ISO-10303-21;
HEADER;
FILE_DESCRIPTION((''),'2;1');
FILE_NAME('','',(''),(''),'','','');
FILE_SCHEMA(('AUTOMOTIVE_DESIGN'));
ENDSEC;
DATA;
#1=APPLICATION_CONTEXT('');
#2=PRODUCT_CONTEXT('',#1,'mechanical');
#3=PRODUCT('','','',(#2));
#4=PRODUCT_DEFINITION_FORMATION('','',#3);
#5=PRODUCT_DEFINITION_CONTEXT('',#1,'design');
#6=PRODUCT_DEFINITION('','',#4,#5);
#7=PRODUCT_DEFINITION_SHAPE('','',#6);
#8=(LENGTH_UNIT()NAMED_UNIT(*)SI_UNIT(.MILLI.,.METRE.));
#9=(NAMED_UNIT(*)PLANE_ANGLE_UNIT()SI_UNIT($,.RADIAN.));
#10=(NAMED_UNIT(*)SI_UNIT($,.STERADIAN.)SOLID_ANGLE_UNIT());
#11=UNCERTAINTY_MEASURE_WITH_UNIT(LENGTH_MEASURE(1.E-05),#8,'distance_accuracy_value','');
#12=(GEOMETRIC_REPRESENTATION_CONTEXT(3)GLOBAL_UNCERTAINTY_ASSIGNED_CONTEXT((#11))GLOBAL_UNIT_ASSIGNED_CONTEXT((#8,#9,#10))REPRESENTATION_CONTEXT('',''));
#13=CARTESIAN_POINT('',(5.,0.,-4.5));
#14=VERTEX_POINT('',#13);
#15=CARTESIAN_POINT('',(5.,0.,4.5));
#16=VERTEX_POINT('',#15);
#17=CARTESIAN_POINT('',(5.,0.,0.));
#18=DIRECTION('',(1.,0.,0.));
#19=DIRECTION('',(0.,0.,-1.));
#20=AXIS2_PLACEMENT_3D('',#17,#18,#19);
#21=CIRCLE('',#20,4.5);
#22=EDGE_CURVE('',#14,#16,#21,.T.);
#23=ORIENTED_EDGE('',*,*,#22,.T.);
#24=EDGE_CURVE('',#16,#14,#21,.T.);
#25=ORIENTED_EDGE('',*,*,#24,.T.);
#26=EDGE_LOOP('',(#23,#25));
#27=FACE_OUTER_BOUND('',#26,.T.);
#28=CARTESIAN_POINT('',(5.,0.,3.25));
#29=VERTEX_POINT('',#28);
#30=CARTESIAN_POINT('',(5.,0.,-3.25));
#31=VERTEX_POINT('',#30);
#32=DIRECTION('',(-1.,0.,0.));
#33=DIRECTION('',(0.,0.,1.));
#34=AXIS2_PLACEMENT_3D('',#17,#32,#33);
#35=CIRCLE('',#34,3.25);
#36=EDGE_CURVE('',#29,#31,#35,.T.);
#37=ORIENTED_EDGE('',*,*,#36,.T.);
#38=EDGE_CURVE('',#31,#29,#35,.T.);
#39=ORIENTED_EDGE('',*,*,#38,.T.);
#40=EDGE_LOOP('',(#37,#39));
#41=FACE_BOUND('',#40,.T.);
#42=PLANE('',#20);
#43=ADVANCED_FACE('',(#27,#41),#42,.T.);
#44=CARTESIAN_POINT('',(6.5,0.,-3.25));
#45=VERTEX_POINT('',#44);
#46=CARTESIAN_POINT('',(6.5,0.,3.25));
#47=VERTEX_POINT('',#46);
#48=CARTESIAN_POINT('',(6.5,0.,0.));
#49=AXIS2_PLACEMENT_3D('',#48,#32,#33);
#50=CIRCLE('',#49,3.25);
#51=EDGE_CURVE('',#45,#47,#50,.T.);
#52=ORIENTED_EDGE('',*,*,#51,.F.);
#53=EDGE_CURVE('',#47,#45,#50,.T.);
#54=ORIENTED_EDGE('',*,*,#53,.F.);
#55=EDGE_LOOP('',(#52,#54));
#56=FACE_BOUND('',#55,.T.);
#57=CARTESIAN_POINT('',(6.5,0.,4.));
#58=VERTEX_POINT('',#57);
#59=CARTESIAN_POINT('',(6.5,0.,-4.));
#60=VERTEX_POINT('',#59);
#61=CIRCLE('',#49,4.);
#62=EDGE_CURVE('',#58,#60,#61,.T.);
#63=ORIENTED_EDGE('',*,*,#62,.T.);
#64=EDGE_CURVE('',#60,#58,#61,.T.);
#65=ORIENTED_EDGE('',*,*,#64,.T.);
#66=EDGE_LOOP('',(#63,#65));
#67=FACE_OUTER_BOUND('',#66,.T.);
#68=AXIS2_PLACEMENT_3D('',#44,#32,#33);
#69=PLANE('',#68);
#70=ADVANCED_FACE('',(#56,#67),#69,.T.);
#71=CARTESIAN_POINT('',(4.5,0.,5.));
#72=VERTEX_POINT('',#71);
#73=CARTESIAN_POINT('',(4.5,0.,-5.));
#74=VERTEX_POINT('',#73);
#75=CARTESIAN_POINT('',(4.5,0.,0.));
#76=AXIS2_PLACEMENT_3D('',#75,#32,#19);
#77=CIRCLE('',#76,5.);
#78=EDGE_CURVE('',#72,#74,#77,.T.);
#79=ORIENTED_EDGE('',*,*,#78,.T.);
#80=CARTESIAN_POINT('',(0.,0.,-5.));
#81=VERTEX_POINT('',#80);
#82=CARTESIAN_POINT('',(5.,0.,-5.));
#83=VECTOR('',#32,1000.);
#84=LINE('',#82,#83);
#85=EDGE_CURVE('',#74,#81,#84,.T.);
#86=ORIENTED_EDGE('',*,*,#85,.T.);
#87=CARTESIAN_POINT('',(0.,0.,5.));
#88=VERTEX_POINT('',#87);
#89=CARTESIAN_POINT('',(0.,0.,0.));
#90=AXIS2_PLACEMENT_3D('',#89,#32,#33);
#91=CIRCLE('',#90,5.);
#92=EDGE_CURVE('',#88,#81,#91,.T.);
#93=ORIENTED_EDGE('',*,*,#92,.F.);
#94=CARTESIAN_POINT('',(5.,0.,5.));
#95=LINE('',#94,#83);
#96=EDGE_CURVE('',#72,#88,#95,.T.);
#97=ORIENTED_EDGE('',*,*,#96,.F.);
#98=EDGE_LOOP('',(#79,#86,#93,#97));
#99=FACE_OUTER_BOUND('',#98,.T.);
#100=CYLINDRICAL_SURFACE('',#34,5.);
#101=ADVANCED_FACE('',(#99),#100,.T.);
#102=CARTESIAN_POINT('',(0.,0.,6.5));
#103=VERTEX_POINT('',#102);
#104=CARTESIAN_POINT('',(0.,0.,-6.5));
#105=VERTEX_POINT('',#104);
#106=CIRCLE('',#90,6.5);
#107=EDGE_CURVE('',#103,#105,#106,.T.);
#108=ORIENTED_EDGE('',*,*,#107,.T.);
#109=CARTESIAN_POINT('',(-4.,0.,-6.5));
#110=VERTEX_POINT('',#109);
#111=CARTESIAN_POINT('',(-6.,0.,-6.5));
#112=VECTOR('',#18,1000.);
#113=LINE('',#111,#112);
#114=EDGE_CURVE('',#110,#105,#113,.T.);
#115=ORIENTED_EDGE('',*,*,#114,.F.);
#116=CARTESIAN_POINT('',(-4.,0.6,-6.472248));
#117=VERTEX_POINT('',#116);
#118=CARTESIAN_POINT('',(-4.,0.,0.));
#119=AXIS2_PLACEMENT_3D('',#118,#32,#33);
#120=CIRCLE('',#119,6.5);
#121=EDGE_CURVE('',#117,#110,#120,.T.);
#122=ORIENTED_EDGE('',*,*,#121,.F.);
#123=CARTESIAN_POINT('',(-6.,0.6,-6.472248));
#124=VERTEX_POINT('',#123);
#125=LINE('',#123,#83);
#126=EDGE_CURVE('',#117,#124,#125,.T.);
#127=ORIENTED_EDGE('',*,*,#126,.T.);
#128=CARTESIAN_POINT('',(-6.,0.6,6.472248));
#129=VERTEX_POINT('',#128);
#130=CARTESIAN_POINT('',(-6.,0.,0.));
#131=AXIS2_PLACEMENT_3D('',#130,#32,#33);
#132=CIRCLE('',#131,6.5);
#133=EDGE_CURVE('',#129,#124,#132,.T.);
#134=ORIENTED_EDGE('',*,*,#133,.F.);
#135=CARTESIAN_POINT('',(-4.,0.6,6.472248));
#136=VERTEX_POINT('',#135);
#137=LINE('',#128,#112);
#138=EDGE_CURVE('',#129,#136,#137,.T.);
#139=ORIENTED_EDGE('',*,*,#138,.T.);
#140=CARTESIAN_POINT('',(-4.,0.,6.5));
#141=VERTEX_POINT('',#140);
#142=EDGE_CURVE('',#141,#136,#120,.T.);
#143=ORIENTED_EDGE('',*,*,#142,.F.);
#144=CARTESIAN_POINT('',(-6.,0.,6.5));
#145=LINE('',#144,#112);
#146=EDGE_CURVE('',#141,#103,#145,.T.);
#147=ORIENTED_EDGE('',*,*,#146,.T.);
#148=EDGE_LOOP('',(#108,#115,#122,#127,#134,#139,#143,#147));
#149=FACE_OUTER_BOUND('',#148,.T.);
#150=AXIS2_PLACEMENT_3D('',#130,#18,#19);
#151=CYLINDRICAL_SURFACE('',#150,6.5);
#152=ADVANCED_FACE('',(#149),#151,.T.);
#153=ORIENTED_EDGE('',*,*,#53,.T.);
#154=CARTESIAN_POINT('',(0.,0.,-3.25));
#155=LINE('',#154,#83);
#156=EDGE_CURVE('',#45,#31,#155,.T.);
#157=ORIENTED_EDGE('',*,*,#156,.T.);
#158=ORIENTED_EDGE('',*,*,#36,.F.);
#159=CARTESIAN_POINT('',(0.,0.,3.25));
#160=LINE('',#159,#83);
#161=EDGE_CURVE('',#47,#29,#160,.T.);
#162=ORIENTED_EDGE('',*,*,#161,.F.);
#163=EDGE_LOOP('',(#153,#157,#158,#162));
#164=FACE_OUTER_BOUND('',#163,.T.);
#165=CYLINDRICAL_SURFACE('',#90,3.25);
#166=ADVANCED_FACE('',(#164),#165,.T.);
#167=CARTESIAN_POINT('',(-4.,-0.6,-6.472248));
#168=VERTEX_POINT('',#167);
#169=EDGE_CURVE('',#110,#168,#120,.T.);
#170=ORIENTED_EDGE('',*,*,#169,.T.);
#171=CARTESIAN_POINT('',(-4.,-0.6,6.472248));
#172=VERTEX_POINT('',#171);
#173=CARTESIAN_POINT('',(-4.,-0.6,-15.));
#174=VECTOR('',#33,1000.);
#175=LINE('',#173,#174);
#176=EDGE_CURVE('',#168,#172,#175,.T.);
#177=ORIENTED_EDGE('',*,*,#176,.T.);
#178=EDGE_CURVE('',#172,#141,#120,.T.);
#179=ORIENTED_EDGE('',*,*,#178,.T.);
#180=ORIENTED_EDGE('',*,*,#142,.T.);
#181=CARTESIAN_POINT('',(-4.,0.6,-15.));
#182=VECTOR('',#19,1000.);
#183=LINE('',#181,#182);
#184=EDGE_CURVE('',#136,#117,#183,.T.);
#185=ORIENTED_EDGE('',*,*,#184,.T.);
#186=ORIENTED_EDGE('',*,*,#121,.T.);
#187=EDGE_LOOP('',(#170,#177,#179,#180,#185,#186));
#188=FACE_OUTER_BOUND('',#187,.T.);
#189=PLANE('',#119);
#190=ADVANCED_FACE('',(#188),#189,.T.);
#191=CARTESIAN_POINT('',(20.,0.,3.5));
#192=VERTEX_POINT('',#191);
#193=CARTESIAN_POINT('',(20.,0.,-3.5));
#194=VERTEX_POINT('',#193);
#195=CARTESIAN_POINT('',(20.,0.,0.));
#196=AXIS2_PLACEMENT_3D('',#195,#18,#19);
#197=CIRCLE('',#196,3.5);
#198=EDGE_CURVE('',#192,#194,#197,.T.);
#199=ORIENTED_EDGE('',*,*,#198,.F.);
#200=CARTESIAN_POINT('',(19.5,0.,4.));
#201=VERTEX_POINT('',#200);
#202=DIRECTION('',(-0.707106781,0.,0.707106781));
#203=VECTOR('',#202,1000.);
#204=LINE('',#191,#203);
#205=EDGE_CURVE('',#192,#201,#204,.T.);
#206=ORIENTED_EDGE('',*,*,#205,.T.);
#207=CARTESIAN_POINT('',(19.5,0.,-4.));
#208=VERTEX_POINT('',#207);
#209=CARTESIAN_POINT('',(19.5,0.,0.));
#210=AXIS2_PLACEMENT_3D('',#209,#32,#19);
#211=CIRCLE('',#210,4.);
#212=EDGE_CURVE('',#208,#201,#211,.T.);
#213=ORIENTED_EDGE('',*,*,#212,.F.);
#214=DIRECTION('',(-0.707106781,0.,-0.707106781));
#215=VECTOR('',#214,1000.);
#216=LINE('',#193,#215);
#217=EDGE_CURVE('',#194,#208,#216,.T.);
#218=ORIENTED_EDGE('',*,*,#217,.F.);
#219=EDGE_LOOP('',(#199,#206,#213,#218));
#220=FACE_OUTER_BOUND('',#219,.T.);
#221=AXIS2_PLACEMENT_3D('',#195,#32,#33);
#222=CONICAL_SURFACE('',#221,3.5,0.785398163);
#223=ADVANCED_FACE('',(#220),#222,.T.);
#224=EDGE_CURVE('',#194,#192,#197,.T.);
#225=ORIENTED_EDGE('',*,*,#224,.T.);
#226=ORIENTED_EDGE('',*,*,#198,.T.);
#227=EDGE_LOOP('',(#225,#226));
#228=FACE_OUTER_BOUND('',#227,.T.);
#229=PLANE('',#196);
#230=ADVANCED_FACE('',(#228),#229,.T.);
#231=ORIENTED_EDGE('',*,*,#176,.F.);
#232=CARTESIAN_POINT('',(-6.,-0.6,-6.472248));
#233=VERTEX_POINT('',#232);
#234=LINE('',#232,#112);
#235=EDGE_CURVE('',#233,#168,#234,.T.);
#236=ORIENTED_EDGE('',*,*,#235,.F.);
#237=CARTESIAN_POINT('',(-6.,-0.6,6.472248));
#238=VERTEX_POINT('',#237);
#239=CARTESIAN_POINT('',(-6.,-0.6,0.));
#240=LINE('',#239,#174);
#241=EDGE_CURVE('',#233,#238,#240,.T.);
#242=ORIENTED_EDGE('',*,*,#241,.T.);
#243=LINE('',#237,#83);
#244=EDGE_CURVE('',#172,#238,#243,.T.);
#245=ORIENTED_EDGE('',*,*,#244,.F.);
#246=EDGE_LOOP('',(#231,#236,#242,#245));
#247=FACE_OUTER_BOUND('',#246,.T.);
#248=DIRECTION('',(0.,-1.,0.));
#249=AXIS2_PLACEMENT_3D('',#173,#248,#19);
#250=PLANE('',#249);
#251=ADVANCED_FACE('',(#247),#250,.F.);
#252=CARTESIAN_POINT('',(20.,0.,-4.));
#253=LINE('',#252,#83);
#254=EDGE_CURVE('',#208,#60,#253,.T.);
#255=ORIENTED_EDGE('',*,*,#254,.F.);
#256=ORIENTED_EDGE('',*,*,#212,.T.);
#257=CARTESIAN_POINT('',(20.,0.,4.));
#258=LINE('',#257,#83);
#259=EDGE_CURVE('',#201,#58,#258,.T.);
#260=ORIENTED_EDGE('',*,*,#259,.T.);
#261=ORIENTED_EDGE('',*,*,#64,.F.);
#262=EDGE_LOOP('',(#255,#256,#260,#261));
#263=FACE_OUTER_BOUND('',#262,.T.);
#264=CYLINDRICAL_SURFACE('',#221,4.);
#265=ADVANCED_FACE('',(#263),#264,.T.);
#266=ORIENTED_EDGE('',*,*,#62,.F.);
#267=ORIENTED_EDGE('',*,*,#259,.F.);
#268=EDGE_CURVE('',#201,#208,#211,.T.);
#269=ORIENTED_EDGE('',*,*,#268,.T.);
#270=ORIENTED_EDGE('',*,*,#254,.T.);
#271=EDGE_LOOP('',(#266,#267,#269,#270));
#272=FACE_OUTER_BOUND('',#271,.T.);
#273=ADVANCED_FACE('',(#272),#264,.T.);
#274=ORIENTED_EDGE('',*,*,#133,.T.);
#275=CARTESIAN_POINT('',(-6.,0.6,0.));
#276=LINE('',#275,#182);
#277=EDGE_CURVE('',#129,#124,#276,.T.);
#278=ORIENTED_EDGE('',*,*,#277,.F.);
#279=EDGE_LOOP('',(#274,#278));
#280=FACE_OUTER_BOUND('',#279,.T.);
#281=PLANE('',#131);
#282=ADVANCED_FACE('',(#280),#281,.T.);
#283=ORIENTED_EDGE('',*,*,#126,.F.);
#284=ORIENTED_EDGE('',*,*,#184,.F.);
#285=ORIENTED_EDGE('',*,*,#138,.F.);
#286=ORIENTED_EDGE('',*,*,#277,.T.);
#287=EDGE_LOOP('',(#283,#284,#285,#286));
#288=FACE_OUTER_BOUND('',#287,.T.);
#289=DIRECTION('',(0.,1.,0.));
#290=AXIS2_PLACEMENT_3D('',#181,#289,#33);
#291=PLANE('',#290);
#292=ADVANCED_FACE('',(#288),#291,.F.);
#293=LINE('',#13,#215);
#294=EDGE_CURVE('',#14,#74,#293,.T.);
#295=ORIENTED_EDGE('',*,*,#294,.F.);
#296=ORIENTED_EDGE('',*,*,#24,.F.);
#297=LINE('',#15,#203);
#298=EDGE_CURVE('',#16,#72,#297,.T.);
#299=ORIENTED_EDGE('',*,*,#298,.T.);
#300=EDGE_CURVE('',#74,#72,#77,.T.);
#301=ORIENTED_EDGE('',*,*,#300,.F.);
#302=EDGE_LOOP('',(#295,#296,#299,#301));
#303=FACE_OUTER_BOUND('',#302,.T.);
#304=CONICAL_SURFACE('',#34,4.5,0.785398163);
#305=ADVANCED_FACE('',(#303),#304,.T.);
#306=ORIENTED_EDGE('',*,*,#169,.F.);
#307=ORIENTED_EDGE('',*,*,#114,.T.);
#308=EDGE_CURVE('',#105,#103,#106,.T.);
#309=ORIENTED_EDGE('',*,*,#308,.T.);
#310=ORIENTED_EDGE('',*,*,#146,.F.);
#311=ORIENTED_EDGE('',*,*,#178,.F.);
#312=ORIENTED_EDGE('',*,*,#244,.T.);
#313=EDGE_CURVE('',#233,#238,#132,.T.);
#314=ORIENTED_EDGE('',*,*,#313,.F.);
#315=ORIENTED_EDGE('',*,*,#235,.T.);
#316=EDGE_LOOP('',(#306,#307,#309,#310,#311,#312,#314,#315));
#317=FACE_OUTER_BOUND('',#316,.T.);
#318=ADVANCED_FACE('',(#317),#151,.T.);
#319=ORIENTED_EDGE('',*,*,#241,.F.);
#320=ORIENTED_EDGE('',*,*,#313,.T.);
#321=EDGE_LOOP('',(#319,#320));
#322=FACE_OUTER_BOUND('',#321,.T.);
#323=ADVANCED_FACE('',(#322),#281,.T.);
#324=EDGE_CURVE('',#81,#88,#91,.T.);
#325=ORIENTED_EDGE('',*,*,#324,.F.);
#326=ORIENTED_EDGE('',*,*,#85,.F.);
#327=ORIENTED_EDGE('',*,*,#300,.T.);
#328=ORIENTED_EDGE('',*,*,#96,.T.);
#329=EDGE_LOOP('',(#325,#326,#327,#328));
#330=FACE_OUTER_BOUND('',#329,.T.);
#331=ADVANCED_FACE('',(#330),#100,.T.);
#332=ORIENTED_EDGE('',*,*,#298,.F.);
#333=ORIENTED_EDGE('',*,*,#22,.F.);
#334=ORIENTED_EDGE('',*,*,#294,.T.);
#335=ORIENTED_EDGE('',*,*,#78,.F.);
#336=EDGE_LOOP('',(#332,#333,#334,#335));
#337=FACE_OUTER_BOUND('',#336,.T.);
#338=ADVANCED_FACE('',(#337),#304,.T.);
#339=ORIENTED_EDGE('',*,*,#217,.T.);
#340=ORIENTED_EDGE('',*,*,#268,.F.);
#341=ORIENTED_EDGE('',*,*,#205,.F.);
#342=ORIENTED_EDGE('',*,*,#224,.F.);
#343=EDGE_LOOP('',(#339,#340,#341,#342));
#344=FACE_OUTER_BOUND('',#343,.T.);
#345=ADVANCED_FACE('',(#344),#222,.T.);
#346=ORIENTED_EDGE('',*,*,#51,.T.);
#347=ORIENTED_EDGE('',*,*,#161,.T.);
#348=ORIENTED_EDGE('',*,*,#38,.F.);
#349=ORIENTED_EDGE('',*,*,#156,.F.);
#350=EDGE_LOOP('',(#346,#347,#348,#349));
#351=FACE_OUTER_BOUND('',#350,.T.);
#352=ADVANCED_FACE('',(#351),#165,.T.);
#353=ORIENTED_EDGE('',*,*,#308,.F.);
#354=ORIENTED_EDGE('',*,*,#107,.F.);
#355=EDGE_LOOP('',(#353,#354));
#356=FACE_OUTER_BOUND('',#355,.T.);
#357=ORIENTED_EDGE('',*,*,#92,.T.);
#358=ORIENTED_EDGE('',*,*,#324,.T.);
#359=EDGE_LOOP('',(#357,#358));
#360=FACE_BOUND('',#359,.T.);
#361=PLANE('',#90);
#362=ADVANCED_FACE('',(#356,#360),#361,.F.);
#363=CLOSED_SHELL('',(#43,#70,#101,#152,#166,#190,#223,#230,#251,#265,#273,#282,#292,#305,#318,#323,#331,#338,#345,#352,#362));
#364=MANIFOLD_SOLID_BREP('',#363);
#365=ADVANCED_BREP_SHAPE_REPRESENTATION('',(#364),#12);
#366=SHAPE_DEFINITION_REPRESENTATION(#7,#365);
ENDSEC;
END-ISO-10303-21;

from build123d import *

# Parameters (mm, degrees)
SKETCH_2_R          = 5
EXTRUDE_1_DEPTH     = 5
SKETCH_5_R          = 6.5
EXTRUDE_2_DEPTH     = 6
SKETCH_6_W          = 30
SKETCH_6_H          = 1.2
CUT_EXTRUDE_1_DEPTH = 2
SKETCH_7_R          = 4
EXTRUDE_3_DEPTH     = 15
CHAMFER_3_SIZE      = 0.5
SKETCH_8_W          = 1.5
SKETCH_8_H          = 1.794916968


with BuildPart() as part:
    # 草图2 → 凸台-拉伸1 (new body)
    with BuildSketch(Plane(origin=(0, 0, 0), x_dir=(0, 0, -1), z_dir=(1, 0, 0))):
        Circle(SKETCH_2_R)
    extrude(amount=EXTRUDE_1_DEPTH)

    # 草图5 → 凸台-拉伸2 (add)
    with BuildSketch(Plane.ZY):
        Circle(SKETCH_5_R)
    extrude(amount=EXTRUDE_2_DEPTH)

    # 草图6 → 切除-拉伸1 (cut)
    with BuildSketch(Plane.ZY.offset(6)):
        Rectangle(SKETCH_6_W, SKETCH_6_H)
    extrude(amount=-CUT_EXTRUDE_1_DEPTH, mode=Mode.SUBTRACT)

    # 草图7 → 凸台-拉伸3 (add)
    with BuildSketch(Plane(origin=(5, 0, 0), x_dir=(0, 0, -1), z_dir=(1, 0, 0))):
        Circle(SKETCH_7_R)
    extrude(amount=EXTRUDE_3_DEPTH)

    # 倒角3
    chamfer_3_edges = [part.edges().sort_by_distance(p)[0] for p in [
        (20, 0, 4),
        (5, 0, 5),
    ]]
    chamfer(chamfer_3_edges, length=CHAMFER_3_SIZE)

    # 草图8 → 切除-旋转1 (revolve, cut)
    with BuildSketch(Plane(origin=(0, 0, 0), x_dir=(1, 0, 0), z_dir=(0, 1, 0)), mode=Mode.PRIVATE) as cut_revolve_1_sk:
        with Locations((5.75, 4.147458484)):
            Rectangle(SKETCH_8_W, SKETCH_8_H)
    revolve(cut_revolve_1_sk.sketch.rotate(Axis((0, 0, 0), (1, 0, 0)), 180), axis=Axis((0, 0, 0), (1, 0, 0)), mode=Mode.SUBTRACT)


solid = part.part
